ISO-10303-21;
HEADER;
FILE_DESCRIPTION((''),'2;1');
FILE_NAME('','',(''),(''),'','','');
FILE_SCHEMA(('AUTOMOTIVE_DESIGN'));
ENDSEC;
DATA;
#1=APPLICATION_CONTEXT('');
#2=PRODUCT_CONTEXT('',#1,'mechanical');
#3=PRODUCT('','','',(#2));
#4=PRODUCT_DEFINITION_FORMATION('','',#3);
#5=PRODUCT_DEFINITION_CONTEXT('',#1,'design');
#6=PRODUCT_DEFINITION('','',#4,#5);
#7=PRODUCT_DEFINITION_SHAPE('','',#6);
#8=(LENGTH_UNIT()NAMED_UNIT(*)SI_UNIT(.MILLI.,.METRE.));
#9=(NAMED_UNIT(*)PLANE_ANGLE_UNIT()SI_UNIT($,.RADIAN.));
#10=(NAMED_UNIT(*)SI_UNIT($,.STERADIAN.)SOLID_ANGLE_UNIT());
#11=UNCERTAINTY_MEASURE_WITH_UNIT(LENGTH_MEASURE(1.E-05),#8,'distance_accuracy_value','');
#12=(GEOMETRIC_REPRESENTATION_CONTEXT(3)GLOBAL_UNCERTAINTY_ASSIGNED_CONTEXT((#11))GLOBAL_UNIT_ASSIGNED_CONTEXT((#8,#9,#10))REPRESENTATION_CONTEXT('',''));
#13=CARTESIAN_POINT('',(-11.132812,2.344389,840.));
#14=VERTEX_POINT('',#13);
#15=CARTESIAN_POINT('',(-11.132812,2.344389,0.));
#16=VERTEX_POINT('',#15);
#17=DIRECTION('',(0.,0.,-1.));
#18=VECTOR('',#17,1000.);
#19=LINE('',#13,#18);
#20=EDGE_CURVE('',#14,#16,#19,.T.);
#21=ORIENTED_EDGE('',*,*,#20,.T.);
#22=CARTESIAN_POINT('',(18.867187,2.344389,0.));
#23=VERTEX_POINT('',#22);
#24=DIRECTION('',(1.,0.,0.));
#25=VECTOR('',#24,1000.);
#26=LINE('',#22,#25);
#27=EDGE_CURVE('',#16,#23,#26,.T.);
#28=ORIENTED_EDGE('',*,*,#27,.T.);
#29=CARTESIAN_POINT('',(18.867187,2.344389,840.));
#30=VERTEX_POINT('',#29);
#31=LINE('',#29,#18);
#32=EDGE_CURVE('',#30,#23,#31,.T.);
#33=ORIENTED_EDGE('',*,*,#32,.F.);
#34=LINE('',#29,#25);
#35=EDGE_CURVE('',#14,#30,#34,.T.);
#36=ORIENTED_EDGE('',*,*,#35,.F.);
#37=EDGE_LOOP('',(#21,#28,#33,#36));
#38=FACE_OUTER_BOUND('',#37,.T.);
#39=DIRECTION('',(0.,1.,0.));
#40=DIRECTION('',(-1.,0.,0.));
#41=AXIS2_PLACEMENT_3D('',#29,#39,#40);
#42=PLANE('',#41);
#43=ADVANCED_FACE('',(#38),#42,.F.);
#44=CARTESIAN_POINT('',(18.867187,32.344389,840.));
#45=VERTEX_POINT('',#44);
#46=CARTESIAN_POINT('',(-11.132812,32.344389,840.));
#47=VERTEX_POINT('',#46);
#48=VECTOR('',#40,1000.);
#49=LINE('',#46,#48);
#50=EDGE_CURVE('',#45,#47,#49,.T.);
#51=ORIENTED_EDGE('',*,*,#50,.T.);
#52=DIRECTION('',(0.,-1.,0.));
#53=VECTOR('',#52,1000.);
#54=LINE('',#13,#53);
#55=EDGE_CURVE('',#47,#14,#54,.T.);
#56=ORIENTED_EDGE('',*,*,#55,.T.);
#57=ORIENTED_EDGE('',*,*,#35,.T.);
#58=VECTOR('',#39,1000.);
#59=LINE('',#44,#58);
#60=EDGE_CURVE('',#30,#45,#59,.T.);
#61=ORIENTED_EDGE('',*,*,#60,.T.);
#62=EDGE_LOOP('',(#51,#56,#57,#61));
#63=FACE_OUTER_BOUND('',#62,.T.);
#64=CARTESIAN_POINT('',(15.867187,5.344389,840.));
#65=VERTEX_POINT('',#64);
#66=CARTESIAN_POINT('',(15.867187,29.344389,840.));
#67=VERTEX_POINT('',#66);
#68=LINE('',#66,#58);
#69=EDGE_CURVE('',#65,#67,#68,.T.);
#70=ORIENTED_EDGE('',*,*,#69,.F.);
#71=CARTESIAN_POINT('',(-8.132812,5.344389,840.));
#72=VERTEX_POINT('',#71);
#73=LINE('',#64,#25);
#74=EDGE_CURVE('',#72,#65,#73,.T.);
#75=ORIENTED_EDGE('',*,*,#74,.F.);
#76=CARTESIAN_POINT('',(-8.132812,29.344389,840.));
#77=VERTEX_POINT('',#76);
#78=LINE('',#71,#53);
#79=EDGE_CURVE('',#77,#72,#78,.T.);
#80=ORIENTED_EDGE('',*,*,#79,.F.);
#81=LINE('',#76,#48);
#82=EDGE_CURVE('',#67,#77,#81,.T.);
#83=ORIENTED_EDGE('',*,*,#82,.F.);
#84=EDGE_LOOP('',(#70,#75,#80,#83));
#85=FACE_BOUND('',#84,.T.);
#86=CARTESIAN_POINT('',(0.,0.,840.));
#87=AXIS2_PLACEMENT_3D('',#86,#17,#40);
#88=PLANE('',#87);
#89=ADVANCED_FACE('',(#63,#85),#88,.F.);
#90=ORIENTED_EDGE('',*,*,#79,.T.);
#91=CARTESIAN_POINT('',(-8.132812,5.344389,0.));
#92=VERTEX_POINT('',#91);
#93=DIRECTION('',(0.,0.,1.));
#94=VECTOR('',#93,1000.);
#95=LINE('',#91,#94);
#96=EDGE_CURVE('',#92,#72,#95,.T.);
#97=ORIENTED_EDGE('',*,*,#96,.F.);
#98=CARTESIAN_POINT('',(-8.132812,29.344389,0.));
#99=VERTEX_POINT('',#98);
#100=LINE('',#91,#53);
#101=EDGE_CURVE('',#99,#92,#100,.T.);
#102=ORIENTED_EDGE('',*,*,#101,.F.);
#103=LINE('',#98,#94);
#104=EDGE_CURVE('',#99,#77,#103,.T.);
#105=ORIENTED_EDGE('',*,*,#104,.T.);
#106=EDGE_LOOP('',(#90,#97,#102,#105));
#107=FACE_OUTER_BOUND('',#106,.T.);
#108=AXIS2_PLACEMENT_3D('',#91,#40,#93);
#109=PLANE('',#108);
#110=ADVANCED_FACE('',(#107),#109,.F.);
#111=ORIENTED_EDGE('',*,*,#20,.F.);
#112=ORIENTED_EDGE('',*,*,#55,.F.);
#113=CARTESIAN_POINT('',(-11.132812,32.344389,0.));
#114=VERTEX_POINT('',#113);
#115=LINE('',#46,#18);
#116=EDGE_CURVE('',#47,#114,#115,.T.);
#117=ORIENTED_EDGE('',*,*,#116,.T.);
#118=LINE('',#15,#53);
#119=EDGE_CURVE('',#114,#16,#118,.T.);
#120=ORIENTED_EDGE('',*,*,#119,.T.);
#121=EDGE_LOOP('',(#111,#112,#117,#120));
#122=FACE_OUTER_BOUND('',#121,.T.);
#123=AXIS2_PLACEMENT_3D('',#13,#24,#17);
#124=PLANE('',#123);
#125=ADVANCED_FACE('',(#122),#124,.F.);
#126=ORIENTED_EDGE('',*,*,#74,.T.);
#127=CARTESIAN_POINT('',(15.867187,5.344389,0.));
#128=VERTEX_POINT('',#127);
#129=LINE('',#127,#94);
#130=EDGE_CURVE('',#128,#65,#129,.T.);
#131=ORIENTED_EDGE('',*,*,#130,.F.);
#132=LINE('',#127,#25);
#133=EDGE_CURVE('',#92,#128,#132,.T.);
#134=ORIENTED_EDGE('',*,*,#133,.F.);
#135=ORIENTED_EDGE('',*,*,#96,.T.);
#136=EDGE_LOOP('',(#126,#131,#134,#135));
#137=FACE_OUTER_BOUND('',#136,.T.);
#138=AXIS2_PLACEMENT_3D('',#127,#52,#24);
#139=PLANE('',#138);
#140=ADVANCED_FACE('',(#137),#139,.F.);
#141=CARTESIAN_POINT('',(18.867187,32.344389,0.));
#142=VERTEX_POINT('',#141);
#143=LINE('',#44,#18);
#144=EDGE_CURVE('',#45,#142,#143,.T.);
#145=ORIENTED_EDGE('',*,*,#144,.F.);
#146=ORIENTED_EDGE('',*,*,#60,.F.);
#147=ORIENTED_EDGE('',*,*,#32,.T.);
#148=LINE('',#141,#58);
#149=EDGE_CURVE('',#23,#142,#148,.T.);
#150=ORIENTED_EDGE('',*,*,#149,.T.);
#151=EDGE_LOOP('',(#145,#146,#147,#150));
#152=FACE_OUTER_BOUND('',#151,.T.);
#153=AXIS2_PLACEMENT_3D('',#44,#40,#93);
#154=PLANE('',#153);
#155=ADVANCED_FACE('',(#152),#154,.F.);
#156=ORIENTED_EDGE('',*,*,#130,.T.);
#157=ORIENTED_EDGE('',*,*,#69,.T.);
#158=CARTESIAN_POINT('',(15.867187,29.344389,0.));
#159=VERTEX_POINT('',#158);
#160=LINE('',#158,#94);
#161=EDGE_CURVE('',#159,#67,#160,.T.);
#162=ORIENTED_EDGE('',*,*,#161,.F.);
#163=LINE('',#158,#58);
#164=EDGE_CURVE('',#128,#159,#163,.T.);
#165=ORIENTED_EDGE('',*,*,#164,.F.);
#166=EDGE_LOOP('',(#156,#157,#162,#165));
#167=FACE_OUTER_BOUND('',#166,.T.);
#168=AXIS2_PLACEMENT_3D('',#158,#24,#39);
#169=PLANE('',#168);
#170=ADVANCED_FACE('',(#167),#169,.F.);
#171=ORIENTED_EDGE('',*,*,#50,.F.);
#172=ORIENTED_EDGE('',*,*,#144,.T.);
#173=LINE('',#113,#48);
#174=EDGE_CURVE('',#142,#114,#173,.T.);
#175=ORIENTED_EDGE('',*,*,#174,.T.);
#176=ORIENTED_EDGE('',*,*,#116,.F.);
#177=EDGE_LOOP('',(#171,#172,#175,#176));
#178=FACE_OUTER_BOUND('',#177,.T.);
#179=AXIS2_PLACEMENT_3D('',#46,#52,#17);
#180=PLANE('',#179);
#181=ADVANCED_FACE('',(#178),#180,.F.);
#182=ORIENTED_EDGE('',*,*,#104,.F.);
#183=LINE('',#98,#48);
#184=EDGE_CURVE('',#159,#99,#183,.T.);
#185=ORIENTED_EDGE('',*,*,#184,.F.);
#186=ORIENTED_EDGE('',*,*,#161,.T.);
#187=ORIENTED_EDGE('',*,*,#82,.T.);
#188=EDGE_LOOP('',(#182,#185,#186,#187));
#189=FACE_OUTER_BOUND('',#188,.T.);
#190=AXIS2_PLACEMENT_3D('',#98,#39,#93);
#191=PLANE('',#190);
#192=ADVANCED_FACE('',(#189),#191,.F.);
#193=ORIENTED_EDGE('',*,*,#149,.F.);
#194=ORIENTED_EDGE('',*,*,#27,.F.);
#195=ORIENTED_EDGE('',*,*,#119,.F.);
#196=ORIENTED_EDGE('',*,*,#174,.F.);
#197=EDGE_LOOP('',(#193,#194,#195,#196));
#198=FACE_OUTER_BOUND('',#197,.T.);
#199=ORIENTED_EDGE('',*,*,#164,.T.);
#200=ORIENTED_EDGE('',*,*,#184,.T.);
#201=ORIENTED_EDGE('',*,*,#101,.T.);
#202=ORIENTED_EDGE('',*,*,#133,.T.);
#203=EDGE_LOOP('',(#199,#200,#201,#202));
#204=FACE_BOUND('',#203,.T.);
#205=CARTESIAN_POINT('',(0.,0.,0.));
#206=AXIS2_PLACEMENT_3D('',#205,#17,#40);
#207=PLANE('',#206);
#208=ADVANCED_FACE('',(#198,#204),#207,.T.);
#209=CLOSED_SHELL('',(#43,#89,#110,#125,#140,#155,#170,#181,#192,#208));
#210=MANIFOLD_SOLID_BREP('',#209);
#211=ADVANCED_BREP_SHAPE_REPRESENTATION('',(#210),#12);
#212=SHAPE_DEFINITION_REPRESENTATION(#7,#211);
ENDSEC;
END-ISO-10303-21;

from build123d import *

# Parameters (mm, degrees)
SKETCH1_W           = 30
SKETCH1_H           = 30
BOSS_EXTRUDE1_DEPTH = 840
SKETCH2_W           = 24
SKETCH2_H           = 24
CUT_EXTRUDE1_DEPTH  = 840


with BuildPart() as part:
    # Sketch1 → Boss-Extrude1 (new body)
    with BuildSketch(Plane.XY):
        with Locations((3.8671875, 17.344389065)):
            Rectangle(SKETCH1_W, SKETCH1_H)
    extrude(amount=BOSS_EXTRUDE1_DEPTH)

    # Sketch2 → Cut-Extrude1 (cut)
    with BuildSketch(Plane.XY.offset(840)):
        with Locations((3.8671875, 17.344389065)):
            Rectangle(SKETCH2_W, SKETCH2_H)
    extrude(amount=-CUT_EXTRUDE1_DEPTH, mode=Mode.SUBTRACT)


solid = part.part
